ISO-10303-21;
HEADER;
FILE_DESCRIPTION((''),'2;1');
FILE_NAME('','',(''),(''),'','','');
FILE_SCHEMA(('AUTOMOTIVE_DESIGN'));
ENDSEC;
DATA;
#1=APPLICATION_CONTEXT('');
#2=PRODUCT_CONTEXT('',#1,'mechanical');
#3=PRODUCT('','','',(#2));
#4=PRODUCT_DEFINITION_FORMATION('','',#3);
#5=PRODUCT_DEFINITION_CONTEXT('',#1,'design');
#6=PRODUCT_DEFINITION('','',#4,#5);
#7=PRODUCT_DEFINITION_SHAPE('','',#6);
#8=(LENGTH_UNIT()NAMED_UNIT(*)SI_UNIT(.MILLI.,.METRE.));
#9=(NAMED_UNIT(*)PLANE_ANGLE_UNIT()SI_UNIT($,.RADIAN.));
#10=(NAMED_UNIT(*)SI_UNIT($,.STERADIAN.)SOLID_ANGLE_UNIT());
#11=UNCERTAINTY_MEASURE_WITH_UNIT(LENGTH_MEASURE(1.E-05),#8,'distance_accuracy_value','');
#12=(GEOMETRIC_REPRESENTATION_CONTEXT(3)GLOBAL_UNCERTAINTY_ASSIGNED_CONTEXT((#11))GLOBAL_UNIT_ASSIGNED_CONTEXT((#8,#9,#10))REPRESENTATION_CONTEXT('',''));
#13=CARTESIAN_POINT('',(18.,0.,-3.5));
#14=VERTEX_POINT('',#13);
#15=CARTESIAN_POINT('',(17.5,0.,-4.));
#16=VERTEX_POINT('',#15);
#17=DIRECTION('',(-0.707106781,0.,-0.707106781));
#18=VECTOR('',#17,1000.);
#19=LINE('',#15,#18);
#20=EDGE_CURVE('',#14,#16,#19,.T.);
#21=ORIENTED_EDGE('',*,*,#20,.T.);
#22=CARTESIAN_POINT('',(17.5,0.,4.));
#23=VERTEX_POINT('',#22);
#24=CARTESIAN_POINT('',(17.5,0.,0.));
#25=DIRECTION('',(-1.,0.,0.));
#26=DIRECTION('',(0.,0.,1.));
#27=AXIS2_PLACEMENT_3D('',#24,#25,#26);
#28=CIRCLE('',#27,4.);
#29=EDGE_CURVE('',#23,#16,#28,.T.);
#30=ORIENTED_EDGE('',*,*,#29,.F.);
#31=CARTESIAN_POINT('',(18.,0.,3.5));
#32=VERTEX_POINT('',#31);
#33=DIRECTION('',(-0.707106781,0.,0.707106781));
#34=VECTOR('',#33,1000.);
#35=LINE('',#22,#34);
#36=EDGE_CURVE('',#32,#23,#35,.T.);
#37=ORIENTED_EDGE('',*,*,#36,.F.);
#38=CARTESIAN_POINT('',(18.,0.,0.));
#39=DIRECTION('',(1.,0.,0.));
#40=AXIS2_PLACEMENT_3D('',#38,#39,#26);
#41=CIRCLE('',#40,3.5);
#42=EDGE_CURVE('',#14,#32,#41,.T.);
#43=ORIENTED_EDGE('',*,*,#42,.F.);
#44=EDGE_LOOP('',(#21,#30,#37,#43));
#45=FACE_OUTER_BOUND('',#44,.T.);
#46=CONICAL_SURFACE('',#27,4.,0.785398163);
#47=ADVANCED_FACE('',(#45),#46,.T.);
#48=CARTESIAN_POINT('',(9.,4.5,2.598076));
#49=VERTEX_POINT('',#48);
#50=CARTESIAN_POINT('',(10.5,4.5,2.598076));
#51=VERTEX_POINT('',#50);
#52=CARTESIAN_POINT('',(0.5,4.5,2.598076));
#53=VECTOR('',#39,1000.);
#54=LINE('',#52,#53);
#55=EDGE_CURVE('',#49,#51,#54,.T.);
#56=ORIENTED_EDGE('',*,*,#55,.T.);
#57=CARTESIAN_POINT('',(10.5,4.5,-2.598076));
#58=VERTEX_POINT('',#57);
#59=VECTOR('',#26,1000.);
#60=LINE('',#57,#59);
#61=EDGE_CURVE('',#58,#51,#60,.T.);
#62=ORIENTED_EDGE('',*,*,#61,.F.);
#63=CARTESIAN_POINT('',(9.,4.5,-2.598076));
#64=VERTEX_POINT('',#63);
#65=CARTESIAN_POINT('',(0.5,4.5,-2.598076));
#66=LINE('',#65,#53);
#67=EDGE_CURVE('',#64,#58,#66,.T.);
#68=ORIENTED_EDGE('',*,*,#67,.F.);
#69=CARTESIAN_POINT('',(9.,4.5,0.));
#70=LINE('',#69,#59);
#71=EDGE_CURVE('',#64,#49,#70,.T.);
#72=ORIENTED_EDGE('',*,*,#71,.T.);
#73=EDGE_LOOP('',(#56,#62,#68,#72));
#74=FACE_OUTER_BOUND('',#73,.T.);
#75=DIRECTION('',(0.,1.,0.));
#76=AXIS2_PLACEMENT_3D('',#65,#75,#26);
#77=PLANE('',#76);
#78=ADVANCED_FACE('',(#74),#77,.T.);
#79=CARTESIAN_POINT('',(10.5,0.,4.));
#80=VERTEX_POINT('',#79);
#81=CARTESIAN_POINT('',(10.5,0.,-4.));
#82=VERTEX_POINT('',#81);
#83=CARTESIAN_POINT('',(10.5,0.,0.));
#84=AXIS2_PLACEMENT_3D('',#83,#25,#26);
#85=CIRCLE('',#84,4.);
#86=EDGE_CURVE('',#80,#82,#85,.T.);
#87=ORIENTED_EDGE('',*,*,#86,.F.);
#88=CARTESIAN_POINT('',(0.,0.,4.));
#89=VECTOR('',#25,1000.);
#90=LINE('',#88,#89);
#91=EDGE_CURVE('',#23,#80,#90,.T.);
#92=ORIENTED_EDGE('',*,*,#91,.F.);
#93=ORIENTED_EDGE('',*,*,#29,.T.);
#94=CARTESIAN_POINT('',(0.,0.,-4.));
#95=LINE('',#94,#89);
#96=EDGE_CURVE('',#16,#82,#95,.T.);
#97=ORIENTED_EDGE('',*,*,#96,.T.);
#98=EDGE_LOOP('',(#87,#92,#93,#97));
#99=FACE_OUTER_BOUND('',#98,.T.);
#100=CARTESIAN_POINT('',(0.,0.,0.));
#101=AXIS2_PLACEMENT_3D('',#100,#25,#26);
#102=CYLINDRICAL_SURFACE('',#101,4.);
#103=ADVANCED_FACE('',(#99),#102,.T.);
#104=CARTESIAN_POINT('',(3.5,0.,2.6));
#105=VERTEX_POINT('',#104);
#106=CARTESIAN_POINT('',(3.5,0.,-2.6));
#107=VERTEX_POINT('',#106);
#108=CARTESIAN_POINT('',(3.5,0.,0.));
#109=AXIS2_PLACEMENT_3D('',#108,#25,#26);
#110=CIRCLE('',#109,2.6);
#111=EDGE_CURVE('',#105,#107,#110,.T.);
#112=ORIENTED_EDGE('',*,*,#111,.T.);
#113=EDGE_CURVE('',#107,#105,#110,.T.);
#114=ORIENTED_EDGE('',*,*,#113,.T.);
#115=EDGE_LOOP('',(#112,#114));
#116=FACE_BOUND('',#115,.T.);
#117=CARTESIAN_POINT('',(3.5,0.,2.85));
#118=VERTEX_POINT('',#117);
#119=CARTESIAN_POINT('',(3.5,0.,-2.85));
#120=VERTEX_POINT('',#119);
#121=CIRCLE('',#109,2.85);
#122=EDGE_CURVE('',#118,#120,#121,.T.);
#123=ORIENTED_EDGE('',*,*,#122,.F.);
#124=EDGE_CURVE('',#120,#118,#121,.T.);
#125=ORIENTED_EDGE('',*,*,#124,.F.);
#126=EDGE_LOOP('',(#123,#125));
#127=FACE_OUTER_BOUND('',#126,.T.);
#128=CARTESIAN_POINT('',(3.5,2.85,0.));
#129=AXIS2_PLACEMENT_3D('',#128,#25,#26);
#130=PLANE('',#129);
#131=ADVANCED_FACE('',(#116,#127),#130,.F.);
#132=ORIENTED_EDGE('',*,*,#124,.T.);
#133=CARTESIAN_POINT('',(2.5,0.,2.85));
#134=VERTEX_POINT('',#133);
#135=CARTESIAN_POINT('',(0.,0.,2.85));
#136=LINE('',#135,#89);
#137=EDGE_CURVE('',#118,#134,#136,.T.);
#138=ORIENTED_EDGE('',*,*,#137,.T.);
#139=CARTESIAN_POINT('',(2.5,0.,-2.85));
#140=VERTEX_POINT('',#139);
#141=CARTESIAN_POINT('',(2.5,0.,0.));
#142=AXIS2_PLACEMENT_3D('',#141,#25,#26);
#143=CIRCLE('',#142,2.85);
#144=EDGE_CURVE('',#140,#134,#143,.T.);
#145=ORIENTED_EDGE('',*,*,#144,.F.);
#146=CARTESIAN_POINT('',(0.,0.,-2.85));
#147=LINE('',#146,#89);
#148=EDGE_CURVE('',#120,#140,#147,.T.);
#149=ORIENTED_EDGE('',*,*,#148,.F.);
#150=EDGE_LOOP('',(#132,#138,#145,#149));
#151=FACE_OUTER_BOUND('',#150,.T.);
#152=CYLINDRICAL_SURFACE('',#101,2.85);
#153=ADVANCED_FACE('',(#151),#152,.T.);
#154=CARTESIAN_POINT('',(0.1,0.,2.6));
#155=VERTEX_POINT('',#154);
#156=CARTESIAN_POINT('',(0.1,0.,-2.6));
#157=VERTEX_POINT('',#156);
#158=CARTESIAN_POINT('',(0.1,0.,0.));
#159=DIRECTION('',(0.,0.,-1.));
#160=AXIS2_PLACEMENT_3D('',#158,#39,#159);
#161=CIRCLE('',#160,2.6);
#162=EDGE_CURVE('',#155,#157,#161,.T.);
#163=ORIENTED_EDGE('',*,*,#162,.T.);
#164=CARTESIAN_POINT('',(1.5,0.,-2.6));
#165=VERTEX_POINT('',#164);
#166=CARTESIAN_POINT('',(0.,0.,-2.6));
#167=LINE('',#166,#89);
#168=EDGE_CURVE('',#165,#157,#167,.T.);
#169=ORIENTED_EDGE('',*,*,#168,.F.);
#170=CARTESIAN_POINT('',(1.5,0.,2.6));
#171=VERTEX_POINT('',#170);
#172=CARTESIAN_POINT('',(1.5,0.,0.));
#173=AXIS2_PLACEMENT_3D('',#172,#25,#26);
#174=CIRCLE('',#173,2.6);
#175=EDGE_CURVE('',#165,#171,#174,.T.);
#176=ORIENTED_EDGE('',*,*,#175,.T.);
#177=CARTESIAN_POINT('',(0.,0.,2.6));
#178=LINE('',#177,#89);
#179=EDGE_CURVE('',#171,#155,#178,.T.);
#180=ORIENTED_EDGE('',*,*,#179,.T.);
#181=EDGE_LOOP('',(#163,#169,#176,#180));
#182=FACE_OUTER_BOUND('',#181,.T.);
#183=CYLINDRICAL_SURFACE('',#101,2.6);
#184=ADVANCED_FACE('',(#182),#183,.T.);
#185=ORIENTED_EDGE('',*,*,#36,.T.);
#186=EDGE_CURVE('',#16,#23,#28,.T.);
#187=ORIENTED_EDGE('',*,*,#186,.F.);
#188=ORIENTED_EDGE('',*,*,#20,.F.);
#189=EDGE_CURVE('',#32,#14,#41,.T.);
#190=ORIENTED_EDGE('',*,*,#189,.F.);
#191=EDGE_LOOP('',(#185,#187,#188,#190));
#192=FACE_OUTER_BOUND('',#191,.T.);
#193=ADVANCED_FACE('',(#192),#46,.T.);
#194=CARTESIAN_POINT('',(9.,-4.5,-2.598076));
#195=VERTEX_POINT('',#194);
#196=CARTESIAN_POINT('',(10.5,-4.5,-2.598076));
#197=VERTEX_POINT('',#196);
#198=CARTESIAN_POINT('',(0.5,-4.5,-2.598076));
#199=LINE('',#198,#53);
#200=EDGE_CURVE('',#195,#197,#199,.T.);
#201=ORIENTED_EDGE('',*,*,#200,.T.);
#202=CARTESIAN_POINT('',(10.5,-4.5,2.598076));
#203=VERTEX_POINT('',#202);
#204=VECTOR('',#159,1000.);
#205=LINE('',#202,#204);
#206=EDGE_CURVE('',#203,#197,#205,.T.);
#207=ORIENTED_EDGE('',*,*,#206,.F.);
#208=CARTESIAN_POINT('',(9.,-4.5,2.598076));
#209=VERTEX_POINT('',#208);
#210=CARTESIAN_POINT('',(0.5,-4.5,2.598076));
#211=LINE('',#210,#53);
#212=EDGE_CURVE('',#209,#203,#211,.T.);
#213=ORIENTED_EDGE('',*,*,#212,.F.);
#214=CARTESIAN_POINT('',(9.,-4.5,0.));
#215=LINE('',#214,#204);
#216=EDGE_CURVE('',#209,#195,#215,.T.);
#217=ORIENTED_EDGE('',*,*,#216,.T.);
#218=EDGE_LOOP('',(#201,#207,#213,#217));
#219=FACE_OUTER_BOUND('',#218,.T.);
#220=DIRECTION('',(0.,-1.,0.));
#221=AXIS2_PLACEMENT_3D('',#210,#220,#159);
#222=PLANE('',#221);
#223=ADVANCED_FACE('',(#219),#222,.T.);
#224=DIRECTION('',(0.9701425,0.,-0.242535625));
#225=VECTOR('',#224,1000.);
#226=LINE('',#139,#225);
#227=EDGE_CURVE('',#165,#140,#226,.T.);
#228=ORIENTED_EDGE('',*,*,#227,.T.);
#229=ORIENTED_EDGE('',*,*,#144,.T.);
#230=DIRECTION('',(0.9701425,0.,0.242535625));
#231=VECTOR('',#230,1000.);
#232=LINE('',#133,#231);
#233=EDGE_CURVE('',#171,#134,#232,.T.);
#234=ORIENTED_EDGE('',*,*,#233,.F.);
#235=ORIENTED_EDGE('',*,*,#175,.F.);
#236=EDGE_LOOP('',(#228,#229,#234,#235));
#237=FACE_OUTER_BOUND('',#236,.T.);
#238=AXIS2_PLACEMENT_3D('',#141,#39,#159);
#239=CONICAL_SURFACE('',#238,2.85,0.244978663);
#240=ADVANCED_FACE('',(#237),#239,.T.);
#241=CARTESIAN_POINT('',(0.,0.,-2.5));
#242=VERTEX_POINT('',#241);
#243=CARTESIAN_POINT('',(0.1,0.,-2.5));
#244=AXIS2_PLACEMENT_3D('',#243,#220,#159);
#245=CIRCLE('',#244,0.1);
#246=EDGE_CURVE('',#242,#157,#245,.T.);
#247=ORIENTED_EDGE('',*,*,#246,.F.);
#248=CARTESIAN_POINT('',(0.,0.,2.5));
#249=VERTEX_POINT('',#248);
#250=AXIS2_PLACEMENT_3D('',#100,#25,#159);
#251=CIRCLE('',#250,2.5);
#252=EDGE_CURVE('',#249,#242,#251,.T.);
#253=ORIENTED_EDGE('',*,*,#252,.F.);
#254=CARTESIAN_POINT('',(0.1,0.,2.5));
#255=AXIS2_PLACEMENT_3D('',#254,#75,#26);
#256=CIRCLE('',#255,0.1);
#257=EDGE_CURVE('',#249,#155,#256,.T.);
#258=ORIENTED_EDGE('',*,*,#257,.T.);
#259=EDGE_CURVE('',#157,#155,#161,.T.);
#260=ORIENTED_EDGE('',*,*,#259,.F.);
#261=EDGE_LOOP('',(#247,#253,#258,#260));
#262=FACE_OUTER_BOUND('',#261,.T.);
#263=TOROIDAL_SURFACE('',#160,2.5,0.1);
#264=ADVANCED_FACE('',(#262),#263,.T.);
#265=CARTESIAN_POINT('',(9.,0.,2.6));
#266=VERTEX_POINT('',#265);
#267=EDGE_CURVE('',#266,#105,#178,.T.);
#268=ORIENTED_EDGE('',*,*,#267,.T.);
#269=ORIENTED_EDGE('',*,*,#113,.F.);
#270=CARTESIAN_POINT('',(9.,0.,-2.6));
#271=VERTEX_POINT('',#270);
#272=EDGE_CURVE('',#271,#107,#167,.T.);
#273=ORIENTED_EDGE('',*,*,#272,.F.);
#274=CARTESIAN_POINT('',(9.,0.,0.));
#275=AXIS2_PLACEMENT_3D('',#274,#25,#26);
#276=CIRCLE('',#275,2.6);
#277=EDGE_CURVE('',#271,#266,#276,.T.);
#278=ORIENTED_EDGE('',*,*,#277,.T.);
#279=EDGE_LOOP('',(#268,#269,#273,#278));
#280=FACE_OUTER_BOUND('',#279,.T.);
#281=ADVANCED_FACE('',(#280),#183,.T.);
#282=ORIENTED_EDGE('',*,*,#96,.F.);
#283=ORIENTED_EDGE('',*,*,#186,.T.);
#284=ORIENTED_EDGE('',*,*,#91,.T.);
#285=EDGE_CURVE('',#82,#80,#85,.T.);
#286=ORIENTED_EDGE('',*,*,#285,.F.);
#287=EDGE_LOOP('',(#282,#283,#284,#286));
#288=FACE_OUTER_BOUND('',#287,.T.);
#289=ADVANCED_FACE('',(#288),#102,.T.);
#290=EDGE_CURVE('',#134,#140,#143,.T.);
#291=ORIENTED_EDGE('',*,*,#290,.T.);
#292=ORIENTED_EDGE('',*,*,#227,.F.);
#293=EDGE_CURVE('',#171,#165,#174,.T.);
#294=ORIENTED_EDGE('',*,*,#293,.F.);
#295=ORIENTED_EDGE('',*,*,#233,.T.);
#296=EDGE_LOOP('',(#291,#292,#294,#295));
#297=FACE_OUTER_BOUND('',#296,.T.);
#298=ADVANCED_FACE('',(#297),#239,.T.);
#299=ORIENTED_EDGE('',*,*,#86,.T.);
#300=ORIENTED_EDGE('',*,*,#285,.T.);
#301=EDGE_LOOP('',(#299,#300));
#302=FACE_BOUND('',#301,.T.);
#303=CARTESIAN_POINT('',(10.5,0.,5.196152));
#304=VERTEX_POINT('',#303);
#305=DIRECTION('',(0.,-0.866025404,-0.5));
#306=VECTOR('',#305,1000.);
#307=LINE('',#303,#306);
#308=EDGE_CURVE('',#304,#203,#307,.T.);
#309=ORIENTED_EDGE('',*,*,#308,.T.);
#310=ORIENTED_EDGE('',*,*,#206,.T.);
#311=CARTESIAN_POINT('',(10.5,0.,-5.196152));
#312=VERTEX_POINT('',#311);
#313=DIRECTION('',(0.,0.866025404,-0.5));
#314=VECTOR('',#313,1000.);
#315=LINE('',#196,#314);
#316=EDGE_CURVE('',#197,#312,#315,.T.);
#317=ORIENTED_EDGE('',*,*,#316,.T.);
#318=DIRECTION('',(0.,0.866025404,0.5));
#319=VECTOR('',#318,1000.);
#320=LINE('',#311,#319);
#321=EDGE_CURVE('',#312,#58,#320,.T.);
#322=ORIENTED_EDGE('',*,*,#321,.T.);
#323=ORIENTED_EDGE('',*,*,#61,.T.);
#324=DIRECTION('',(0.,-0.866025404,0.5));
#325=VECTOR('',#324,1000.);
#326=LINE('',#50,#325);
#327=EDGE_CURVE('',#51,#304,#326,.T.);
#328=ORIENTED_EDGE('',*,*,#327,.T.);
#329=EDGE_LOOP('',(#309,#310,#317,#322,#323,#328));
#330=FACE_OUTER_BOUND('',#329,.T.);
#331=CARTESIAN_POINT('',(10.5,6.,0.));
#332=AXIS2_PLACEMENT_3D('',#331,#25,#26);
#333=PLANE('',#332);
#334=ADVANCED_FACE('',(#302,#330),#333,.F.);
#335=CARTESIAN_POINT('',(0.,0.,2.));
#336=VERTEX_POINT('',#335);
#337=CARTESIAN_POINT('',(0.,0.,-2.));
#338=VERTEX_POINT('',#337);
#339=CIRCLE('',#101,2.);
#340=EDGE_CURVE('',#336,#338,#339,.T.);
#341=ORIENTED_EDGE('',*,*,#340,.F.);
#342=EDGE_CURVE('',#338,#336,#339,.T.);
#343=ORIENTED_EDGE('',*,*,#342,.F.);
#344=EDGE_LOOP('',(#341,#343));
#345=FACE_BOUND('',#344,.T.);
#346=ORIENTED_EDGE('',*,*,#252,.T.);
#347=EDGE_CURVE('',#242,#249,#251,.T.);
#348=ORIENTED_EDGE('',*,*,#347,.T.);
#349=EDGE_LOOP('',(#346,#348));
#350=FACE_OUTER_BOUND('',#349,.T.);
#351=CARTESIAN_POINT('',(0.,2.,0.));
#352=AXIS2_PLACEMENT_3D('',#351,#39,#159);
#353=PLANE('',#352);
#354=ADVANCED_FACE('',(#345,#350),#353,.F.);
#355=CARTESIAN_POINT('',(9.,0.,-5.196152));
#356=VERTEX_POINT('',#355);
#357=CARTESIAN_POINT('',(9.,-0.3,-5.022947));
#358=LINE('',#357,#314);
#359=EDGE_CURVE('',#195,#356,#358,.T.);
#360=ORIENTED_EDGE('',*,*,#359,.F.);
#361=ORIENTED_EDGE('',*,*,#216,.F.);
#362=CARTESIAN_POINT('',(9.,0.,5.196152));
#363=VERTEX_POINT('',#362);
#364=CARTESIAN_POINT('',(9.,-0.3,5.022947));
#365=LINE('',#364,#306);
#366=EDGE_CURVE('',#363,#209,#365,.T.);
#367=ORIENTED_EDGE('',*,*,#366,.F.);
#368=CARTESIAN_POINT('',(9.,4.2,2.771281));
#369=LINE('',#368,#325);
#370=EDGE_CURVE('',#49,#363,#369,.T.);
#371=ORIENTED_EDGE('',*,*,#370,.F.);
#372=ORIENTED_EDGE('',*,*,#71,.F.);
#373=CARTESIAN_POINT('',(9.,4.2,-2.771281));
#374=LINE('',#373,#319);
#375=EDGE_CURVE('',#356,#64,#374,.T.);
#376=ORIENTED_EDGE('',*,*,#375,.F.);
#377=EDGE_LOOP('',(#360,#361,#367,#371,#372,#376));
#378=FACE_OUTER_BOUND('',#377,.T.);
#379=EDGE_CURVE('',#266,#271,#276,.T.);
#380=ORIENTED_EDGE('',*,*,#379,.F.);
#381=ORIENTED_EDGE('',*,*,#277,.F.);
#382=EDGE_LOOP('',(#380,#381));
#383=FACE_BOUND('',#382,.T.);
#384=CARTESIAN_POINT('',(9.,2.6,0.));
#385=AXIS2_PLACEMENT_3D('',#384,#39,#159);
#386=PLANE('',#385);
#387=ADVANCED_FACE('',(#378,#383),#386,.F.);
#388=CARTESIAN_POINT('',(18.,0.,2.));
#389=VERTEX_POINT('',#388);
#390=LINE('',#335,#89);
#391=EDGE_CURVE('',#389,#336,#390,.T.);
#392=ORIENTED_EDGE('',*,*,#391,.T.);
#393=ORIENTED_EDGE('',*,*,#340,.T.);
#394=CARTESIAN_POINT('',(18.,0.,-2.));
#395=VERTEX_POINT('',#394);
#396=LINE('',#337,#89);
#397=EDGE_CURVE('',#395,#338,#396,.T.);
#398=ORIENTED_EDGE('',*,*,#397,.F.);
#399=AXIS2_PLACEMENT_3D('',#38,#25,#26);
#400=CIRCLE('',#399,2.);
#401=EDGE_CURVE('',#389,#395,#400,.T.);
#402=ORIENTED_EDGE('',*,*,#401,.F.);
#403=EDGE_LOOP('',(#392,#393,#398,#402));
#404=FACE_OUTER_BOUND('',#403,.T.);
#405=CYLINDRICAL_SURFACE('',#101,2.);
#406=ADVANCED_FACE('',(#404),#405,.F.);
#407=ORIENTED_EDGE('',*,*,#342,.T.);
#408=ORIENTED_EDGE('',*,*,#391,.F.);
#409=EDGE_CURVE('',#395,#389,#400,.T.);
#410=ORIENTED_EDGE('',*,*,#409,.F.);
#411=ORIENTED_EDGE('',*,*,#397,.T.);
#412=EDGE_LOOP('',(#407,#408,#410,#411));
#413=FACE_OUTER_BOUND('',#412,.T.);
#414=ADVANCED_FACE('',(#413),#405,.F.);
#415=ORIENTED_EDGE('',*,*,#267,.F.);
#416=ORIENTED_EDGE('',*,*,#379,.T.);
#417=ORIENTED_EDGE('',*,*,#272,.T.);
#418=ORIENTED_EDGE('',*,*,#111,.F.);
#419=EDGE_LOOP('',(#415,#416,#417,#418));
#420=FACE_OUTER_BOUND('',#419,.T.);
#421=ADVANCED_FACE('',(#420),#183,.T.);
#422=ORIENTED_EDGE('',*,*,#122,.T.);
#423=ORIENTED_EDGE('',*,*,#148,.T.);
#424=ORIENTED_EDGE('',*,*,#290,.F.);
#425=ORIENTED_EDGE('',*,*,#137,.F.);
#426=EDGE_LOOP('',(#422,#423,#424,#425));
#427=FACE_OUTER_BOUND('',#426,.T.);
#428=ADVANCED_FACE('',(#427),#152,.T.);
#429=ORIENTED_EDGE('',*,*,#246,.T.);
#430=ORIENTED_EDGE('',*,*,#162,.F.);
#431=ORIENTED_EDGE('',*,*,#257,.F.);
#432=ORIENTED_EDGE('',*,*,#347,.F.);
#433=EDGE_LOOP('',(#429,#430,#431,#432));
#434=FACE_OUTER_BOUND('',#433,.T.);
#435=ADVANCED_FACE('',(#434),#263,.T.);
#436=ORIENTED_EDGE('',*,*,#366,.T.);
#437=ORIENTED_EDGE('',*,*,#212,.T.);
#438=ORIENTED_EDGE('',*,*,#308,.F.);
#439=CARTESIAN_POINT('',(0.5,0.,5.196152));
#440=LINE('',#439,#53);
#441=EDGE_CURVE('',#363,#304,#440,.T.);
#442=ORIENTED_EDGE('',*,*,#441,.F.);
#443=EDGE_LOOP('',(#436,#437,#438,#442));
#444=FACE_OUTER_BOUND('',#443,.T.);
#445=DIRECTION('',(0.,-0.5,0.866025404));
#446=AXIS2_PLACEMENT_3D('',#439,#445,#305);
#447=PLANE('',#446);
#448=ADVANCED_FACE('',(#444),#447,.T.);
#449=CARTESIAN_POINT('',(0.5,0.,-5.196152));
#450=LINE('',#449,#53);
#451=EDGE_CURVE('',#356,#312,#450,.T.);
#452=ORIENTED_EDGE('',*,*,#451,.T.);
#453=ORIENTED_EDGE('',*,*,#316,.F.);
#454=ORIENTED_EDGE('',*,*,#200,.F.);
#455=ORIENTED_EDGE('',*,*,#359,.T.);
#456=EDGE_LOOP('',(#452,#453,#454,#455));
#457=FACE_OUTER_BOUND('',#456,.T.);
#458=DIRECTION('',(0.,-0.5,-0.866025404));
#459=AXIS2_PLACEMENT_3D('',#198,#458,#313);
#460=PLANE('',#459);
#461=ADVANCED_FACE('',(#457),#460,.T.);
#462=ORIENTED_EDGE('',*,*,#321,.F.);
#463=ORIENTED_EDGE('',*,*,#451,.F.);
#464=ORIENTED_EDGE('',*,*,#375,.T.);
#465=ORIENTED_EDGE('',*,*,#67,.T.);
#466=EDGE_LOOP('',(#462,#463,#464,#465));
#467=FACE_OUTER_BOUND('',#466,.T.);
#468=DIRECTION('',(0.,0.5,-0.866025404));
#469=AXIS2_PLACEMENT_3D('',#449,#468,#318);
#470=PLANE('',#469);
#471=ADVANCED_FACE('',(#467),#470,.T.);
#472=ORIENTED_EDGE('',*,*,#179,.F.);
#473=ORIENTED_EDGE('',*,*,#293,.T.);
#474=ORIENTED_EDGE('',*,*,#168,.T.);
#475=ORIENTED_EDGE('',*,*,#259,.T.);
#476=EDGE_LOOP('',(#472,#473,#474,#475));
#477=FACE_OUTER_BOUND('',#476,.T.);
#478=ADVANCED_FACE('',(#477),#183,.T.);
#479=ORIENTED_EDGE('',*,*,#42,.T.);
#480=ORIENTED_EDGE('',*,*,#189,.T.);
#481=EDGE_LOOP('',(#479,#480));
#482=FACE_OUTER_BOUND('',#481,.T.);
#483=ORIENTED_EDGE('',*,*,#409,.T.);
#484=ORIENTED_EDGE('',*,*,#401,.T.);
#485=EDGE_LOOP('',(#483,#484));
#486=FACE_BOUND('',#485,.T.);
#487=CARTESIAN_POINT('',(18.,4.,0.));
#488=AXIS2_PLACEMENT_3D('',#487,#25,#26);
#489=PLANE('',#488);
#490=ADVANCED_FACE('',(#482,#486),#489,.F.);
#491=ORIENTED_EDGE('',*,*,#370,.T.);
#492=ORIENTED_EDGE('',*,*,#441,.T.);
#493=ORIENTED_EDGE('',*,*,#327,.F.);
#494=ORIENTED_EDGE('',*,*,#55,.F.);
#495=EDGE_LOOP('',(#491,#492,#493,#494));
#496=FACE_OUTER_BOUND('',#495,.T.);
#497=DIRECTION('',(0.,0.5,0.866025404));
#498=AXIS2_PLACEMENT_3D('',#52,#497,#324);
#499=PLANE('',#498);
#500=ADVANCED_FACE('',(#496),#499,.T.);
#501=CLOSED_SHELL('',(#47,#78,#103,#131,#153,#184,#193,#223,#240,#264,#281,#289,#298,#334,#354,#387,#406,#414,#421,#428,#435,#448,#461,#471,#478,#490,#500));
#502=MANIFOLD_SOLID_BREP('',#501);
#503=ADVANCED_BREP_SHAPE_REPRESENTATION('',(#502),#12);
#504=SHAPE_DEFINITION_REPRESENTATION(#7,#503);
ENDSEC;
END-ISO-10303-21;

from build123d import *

# Parameters (mm, degrees)
SKETCH2_OUTSIDE_W  = 18.948
SKETCH2_OUTSIDE_H  = 18.948
CUT_EXTRUDE3_DEPTH = 10
FILLET1_R          = 0.1
CHAMFER1_SIZE      = 0.5


with BuildPart() as part:
    # Sketch1 → Revolve1 (revolve)
    with BuildSketch(Plane.XY, mode=Mode.PRIVATE) as revolve1_sk:
        Polygon((0, 2), (18, 2), (18, 4), (10.5, 4), (10.5, 6), (9, 6), (9, 2.6), (3.5, 2.6), (3.5, 2.85), (2.5, 2.85), (1.5, 2.6), (0, 2.6), align=None)
    revolve(revolve1_sk.sketch.rotate(Axis((0, 0, 0), (1, 0, 0)), 90), axis=Axis((0, 0, 0), (1, 0, 0)))

    # Sketch2 outside → Cut-Extrude3 (cut)
    with BuildSketch(Plane(origin=(10.5, 0, 0), x_dir=(0, 0, -1), z_dir=(1, 0, 0))):
        Rectangle(SKETCH2_OUTSIDE_W, SKETCH2_OUTSIDE_H)
        Polygon((2.598076211, -4.5), (5.196152423, 0), (2.598076211, 4.5), (-2.598076211, 4.5), (-5.196152423, 0), (-2.598076211, -4.5), align=None, mode=Mode.SUBTRACT)
    extrude(amount=-CUT_EXTRUDE3_DEPTH, mode=Mode.SUBTRACT)

    # Fillet1
    fillet1_edges = [part.edges().sort_by_distance(p)[0] for p in [
        (0, 0, -2.6),
    ]]
    fillet(fillet1_edges, radius=FILLET1_R)

    # Chamfer1
    chamfer1_edges = [part.edges().sort_by_distance(p)[0] for p in [
        (18, 0, -4),
    ]]
    chamfer(chamfer1_edges, length=CHAMFER1_SIZE)


solid = part.part
